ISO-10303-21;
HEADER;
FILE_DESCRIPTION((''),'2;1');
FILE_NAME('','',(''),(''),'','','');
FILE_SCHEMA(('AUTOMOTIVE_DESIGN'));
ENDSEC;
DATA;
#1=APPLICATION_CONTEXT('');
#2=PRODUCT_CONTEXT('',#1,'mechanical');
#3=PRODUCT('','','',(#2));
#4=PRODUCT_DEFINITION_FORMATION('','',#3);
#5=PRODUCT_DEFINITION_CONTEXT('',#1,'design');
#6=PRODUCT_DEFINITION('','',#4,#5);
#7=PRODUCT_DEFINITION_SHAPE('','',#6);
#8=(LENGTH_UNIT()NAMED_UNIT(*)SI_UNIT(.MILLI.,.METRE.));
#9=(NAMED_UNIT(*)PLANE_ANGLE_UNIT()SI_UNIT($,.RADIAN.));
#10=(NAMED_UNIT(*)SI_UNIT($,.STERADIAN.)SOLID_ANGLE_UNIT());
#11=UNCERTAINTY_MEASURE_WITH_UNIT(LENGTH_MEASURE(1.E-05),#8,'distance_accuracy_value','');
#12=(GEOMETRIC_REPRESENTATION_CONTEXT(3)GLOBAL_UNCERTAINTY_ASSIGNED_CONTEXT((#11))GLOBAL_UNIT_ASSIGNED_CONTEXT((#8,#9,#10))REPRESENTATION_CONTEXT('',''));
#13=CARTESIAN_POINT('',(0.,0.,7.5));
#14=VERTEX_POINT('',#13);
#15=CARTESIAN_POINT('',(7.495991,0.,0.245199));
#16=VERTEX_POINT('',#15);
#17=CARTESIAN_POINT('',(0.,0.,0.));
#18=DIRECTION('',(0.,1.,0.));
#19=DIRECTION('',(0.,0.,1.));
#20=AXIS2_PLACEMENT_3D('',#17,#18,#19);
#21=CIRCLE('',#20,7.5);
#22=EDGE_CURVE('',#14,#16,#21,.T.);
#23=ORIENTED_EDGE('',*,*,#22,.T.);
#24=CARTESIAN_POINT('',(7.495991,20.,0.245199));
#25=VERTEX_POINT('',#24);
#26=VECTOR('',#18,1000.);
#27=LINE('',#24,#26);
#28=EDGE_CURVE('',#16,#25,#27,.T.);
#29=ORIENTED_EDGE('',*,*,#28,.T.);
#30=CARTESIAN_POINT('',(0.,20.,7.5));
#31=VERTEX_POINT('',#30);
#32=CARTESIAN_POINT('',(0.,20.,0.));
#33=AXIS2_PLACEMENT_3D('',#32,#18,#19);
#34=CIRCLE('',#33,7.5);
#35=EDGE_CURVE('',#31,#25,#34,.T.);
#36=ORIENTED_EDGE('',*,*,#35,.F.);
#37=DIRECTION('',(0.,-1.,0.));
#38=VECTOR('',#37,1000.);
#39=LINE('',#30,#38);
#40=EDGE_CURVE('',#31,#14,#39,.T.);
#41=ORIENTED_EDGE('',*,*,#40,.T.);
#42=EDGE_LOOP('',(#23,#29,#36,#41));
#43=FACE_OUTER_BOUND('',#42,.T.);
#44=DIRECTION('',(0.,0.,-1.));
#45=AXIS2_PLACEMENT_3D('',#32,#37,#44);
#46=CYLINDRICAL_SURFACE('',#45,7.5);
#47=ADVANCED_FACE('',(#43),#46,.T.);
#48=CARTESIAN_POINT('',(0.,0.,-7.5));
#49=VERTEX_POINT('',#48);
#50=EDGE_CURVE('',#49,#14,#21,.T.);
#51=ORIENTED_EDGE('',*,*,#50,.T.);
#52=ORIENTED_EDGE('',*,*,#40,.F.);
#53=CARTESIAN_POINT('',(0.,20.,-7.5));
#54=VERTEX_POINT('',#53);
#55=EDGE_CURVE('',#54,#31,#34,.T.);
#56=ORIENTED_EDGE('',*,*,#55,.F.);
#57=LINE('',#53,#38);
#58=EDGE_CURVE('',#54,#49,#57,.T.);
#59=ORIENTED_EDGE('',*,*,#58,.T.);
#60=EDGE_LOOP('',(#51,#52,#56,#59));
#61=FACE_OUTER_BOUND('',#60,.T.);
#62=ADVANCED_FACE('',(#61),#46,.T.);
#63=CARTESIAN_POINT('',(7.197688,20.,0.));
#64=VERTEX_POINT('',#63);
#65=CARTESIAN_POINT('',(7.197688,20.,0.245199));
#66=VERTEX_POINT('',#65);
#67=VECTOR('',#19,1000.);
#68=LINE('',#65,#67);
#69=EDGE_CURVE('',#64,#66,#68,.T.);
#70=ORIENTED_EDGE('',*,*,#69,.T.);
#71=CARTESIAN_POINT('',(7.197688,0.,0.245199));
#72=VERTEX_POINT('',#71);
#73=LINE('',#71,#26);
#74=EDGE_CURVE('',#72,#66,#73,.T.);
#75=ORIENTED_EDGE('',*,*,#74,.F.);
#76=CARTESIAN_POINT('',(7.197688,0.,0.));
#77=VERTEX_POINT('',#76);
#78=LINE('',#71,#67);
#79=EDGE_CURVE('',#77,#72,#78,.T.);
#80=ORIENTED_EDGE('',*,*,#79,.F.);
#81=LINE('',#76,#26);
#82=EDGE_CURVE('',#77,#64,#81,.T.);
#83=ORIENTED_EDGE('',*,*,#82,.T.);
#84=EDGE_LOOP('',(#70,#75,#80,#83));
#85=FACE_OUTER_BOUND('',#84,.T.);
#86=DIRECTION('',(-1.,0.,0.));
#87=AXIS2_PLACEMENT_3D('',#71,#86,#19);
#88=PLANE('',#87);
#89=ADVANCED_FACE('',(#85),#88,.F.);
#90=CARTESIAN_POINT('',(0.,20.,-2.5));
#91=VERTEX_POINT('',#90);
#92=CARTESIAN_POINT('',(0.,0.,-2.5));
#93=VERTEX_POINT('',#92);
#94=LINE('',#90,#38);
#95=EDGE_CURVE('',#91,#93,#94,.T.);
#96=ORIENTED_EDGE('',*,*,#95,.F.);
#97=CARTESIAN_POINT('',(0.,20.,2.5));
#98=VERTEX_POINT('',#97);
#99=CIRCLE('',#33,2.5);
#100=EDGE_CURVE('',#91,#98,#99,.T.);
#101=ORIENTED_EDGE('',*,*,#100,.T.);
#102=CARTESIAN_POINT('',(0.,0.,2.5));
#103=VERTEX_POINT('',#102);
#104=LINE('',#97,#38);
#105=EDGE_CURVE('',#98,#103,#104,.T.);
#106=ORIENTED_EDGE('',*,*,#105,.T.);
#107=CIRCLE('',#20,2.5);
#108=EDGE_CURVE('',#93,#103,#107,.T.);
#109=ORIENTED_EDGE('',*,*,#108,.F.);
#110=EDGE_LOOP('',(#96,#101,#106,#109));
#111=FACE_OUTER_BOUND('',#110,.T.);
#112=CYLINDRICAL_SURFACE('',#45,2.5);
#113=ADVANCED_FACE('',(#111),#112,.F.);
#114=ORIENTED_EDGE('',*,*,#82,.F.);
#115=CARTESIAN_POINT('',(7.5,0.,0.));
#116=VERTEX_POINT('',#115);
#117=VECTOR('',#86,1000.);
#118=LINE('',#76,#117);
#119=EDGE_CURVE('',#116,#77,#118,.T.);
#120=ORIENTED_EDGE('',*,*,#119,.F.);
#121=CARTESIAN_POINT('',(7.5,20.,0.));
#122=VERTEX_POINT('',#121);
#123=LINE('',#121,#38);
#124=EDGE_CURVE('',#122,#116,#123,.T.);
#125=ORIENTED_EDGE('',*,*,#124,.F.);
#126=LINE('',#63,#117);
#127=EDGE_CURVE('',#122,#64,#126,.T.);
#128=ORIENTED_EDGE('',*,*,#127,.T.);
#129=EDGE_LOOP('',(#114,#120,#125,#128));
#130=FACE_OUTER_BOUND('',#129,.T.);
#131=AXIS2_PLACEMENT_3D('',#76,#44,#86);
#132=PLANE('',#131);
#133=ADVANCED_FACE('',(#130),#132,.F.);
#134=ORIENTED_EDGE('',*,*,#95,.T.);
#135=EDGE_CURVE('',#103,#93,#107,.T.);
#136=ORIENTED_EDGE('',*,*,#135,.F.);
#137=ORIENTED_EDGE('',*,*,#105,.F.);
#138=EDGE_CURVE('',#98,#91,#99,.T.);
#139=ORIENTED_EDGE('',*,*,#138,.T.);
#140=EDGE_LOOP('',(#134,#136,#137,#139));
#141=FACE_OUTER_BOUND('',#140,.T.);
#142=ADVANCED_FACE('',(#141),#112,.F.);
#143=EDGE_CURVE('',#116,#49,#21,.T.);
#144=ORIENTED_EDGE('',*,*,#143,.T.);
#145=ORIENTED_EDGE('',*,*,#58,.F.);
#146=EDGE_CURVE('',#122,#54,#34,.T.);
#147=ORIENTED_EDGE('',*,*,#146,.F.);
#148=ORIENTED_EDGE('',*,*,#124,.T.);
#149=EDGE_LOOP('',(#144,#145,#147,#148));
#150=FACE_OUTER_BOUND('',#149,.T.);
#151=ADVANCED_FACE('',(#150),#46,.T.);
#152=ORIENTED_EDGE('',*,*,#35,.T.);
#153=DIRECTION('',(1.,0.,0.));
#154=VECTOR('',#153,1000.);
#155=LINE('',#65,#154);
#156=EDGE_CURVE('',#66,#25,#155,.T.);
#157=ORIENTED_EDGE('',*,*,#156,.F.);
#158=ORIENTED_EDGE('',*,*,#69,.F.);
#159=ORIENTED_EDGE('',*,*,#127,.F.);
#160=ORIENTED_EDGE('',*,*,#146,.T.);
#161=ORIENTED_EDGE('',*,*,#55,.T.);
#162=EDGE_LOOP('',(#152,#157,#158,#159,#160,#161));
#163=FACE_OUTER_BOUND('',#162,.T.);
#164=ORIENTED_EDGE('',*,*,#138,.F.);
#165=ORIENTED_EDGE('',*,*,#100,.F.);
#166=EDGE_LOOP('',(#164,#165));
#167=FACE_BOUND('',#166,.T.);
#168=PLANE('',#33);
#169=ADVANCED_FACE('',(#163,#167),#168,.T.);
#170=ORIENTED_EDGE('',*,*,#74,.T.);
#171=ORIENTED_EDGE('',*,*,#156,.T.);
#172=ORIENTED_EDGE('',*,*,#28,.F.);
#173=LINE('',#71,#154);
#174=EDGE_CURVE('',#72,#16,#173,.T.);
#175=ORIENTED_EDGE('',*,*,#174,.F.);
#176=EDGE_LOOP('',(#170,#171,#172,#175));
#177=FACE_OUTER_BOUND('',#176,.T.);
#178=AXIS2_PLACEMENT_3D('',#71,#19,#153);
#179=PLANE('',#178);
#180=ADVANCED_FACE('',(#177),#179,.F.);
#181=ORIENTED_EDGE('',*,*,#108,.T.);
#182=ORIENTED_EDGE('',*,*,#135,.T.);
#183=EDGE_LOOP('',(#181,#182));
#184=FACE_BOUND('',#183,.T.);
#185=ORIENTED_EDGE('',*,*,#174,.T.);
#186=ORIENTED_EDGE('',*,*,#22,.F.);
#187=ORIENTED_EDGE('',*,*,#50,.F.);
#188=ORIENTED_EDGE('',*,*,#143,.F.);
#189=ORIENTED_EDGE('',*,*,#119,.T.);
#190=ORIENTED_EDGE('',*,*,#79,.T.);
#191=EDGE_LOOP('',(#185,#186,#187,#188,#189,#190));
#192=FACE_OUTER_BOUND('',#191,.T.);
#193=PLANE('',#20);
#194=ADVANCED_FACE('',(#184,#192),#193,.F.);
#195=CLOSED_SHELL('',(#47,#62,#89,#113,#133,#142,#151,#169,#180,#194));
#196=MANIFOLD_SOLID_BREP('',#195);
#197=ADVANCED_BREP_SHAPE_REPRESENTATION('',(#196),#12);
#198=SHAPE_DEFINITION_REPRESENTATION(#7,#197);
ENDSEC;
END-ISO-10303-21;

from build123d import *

# Parameters (mm, degrees)
SKETCH1_R           = 7.5
SKETCH1_R_2         = 2.5
BOSS_EXTRUDE1_DEPTH = 20
SKETCH2_W           = 0.602620298
SKETCH2_H           = 0.245198841
CUT_EXTRUDE1_DEPTH  = 23.638462845


with BuildPart() as part:
    # Sketch1 → Boss-Extrude1 (new body)
    with BuildSketch(Plane(origin=(0, 0, 0), x_dir=(1, 0, 0), z_dir=(0, 1, 0))):
        with Locations(Location((0, 0, 0), (0, 0, 270))):
            Circle(SKETCH1_R)
        with Locations(Location((0, 0, 0), (0, 0, 270))):
            Circle(SKETCH1_R_2, mode=Mode.SUBTRACT)
    extrude(amount=BOSS_EXTRUDE1_DEPTH)

    # Sketch2 → Cut-Extrude1 (cut, through all)
    with BuildSketch(Plane(origin=(0, 20, 0), x_dir=(1, 0, 0), z_dir=(0, 1, 0))):
        with Locations((7.498997892, -0.122599421)):
            Rectangle(SKETCH2_W, SKETCH2_H)
    extrude(amount=-CUT_EXTRUDE1_DEPTH, mode=Mode.SUBTRACT)


solid = part.part
